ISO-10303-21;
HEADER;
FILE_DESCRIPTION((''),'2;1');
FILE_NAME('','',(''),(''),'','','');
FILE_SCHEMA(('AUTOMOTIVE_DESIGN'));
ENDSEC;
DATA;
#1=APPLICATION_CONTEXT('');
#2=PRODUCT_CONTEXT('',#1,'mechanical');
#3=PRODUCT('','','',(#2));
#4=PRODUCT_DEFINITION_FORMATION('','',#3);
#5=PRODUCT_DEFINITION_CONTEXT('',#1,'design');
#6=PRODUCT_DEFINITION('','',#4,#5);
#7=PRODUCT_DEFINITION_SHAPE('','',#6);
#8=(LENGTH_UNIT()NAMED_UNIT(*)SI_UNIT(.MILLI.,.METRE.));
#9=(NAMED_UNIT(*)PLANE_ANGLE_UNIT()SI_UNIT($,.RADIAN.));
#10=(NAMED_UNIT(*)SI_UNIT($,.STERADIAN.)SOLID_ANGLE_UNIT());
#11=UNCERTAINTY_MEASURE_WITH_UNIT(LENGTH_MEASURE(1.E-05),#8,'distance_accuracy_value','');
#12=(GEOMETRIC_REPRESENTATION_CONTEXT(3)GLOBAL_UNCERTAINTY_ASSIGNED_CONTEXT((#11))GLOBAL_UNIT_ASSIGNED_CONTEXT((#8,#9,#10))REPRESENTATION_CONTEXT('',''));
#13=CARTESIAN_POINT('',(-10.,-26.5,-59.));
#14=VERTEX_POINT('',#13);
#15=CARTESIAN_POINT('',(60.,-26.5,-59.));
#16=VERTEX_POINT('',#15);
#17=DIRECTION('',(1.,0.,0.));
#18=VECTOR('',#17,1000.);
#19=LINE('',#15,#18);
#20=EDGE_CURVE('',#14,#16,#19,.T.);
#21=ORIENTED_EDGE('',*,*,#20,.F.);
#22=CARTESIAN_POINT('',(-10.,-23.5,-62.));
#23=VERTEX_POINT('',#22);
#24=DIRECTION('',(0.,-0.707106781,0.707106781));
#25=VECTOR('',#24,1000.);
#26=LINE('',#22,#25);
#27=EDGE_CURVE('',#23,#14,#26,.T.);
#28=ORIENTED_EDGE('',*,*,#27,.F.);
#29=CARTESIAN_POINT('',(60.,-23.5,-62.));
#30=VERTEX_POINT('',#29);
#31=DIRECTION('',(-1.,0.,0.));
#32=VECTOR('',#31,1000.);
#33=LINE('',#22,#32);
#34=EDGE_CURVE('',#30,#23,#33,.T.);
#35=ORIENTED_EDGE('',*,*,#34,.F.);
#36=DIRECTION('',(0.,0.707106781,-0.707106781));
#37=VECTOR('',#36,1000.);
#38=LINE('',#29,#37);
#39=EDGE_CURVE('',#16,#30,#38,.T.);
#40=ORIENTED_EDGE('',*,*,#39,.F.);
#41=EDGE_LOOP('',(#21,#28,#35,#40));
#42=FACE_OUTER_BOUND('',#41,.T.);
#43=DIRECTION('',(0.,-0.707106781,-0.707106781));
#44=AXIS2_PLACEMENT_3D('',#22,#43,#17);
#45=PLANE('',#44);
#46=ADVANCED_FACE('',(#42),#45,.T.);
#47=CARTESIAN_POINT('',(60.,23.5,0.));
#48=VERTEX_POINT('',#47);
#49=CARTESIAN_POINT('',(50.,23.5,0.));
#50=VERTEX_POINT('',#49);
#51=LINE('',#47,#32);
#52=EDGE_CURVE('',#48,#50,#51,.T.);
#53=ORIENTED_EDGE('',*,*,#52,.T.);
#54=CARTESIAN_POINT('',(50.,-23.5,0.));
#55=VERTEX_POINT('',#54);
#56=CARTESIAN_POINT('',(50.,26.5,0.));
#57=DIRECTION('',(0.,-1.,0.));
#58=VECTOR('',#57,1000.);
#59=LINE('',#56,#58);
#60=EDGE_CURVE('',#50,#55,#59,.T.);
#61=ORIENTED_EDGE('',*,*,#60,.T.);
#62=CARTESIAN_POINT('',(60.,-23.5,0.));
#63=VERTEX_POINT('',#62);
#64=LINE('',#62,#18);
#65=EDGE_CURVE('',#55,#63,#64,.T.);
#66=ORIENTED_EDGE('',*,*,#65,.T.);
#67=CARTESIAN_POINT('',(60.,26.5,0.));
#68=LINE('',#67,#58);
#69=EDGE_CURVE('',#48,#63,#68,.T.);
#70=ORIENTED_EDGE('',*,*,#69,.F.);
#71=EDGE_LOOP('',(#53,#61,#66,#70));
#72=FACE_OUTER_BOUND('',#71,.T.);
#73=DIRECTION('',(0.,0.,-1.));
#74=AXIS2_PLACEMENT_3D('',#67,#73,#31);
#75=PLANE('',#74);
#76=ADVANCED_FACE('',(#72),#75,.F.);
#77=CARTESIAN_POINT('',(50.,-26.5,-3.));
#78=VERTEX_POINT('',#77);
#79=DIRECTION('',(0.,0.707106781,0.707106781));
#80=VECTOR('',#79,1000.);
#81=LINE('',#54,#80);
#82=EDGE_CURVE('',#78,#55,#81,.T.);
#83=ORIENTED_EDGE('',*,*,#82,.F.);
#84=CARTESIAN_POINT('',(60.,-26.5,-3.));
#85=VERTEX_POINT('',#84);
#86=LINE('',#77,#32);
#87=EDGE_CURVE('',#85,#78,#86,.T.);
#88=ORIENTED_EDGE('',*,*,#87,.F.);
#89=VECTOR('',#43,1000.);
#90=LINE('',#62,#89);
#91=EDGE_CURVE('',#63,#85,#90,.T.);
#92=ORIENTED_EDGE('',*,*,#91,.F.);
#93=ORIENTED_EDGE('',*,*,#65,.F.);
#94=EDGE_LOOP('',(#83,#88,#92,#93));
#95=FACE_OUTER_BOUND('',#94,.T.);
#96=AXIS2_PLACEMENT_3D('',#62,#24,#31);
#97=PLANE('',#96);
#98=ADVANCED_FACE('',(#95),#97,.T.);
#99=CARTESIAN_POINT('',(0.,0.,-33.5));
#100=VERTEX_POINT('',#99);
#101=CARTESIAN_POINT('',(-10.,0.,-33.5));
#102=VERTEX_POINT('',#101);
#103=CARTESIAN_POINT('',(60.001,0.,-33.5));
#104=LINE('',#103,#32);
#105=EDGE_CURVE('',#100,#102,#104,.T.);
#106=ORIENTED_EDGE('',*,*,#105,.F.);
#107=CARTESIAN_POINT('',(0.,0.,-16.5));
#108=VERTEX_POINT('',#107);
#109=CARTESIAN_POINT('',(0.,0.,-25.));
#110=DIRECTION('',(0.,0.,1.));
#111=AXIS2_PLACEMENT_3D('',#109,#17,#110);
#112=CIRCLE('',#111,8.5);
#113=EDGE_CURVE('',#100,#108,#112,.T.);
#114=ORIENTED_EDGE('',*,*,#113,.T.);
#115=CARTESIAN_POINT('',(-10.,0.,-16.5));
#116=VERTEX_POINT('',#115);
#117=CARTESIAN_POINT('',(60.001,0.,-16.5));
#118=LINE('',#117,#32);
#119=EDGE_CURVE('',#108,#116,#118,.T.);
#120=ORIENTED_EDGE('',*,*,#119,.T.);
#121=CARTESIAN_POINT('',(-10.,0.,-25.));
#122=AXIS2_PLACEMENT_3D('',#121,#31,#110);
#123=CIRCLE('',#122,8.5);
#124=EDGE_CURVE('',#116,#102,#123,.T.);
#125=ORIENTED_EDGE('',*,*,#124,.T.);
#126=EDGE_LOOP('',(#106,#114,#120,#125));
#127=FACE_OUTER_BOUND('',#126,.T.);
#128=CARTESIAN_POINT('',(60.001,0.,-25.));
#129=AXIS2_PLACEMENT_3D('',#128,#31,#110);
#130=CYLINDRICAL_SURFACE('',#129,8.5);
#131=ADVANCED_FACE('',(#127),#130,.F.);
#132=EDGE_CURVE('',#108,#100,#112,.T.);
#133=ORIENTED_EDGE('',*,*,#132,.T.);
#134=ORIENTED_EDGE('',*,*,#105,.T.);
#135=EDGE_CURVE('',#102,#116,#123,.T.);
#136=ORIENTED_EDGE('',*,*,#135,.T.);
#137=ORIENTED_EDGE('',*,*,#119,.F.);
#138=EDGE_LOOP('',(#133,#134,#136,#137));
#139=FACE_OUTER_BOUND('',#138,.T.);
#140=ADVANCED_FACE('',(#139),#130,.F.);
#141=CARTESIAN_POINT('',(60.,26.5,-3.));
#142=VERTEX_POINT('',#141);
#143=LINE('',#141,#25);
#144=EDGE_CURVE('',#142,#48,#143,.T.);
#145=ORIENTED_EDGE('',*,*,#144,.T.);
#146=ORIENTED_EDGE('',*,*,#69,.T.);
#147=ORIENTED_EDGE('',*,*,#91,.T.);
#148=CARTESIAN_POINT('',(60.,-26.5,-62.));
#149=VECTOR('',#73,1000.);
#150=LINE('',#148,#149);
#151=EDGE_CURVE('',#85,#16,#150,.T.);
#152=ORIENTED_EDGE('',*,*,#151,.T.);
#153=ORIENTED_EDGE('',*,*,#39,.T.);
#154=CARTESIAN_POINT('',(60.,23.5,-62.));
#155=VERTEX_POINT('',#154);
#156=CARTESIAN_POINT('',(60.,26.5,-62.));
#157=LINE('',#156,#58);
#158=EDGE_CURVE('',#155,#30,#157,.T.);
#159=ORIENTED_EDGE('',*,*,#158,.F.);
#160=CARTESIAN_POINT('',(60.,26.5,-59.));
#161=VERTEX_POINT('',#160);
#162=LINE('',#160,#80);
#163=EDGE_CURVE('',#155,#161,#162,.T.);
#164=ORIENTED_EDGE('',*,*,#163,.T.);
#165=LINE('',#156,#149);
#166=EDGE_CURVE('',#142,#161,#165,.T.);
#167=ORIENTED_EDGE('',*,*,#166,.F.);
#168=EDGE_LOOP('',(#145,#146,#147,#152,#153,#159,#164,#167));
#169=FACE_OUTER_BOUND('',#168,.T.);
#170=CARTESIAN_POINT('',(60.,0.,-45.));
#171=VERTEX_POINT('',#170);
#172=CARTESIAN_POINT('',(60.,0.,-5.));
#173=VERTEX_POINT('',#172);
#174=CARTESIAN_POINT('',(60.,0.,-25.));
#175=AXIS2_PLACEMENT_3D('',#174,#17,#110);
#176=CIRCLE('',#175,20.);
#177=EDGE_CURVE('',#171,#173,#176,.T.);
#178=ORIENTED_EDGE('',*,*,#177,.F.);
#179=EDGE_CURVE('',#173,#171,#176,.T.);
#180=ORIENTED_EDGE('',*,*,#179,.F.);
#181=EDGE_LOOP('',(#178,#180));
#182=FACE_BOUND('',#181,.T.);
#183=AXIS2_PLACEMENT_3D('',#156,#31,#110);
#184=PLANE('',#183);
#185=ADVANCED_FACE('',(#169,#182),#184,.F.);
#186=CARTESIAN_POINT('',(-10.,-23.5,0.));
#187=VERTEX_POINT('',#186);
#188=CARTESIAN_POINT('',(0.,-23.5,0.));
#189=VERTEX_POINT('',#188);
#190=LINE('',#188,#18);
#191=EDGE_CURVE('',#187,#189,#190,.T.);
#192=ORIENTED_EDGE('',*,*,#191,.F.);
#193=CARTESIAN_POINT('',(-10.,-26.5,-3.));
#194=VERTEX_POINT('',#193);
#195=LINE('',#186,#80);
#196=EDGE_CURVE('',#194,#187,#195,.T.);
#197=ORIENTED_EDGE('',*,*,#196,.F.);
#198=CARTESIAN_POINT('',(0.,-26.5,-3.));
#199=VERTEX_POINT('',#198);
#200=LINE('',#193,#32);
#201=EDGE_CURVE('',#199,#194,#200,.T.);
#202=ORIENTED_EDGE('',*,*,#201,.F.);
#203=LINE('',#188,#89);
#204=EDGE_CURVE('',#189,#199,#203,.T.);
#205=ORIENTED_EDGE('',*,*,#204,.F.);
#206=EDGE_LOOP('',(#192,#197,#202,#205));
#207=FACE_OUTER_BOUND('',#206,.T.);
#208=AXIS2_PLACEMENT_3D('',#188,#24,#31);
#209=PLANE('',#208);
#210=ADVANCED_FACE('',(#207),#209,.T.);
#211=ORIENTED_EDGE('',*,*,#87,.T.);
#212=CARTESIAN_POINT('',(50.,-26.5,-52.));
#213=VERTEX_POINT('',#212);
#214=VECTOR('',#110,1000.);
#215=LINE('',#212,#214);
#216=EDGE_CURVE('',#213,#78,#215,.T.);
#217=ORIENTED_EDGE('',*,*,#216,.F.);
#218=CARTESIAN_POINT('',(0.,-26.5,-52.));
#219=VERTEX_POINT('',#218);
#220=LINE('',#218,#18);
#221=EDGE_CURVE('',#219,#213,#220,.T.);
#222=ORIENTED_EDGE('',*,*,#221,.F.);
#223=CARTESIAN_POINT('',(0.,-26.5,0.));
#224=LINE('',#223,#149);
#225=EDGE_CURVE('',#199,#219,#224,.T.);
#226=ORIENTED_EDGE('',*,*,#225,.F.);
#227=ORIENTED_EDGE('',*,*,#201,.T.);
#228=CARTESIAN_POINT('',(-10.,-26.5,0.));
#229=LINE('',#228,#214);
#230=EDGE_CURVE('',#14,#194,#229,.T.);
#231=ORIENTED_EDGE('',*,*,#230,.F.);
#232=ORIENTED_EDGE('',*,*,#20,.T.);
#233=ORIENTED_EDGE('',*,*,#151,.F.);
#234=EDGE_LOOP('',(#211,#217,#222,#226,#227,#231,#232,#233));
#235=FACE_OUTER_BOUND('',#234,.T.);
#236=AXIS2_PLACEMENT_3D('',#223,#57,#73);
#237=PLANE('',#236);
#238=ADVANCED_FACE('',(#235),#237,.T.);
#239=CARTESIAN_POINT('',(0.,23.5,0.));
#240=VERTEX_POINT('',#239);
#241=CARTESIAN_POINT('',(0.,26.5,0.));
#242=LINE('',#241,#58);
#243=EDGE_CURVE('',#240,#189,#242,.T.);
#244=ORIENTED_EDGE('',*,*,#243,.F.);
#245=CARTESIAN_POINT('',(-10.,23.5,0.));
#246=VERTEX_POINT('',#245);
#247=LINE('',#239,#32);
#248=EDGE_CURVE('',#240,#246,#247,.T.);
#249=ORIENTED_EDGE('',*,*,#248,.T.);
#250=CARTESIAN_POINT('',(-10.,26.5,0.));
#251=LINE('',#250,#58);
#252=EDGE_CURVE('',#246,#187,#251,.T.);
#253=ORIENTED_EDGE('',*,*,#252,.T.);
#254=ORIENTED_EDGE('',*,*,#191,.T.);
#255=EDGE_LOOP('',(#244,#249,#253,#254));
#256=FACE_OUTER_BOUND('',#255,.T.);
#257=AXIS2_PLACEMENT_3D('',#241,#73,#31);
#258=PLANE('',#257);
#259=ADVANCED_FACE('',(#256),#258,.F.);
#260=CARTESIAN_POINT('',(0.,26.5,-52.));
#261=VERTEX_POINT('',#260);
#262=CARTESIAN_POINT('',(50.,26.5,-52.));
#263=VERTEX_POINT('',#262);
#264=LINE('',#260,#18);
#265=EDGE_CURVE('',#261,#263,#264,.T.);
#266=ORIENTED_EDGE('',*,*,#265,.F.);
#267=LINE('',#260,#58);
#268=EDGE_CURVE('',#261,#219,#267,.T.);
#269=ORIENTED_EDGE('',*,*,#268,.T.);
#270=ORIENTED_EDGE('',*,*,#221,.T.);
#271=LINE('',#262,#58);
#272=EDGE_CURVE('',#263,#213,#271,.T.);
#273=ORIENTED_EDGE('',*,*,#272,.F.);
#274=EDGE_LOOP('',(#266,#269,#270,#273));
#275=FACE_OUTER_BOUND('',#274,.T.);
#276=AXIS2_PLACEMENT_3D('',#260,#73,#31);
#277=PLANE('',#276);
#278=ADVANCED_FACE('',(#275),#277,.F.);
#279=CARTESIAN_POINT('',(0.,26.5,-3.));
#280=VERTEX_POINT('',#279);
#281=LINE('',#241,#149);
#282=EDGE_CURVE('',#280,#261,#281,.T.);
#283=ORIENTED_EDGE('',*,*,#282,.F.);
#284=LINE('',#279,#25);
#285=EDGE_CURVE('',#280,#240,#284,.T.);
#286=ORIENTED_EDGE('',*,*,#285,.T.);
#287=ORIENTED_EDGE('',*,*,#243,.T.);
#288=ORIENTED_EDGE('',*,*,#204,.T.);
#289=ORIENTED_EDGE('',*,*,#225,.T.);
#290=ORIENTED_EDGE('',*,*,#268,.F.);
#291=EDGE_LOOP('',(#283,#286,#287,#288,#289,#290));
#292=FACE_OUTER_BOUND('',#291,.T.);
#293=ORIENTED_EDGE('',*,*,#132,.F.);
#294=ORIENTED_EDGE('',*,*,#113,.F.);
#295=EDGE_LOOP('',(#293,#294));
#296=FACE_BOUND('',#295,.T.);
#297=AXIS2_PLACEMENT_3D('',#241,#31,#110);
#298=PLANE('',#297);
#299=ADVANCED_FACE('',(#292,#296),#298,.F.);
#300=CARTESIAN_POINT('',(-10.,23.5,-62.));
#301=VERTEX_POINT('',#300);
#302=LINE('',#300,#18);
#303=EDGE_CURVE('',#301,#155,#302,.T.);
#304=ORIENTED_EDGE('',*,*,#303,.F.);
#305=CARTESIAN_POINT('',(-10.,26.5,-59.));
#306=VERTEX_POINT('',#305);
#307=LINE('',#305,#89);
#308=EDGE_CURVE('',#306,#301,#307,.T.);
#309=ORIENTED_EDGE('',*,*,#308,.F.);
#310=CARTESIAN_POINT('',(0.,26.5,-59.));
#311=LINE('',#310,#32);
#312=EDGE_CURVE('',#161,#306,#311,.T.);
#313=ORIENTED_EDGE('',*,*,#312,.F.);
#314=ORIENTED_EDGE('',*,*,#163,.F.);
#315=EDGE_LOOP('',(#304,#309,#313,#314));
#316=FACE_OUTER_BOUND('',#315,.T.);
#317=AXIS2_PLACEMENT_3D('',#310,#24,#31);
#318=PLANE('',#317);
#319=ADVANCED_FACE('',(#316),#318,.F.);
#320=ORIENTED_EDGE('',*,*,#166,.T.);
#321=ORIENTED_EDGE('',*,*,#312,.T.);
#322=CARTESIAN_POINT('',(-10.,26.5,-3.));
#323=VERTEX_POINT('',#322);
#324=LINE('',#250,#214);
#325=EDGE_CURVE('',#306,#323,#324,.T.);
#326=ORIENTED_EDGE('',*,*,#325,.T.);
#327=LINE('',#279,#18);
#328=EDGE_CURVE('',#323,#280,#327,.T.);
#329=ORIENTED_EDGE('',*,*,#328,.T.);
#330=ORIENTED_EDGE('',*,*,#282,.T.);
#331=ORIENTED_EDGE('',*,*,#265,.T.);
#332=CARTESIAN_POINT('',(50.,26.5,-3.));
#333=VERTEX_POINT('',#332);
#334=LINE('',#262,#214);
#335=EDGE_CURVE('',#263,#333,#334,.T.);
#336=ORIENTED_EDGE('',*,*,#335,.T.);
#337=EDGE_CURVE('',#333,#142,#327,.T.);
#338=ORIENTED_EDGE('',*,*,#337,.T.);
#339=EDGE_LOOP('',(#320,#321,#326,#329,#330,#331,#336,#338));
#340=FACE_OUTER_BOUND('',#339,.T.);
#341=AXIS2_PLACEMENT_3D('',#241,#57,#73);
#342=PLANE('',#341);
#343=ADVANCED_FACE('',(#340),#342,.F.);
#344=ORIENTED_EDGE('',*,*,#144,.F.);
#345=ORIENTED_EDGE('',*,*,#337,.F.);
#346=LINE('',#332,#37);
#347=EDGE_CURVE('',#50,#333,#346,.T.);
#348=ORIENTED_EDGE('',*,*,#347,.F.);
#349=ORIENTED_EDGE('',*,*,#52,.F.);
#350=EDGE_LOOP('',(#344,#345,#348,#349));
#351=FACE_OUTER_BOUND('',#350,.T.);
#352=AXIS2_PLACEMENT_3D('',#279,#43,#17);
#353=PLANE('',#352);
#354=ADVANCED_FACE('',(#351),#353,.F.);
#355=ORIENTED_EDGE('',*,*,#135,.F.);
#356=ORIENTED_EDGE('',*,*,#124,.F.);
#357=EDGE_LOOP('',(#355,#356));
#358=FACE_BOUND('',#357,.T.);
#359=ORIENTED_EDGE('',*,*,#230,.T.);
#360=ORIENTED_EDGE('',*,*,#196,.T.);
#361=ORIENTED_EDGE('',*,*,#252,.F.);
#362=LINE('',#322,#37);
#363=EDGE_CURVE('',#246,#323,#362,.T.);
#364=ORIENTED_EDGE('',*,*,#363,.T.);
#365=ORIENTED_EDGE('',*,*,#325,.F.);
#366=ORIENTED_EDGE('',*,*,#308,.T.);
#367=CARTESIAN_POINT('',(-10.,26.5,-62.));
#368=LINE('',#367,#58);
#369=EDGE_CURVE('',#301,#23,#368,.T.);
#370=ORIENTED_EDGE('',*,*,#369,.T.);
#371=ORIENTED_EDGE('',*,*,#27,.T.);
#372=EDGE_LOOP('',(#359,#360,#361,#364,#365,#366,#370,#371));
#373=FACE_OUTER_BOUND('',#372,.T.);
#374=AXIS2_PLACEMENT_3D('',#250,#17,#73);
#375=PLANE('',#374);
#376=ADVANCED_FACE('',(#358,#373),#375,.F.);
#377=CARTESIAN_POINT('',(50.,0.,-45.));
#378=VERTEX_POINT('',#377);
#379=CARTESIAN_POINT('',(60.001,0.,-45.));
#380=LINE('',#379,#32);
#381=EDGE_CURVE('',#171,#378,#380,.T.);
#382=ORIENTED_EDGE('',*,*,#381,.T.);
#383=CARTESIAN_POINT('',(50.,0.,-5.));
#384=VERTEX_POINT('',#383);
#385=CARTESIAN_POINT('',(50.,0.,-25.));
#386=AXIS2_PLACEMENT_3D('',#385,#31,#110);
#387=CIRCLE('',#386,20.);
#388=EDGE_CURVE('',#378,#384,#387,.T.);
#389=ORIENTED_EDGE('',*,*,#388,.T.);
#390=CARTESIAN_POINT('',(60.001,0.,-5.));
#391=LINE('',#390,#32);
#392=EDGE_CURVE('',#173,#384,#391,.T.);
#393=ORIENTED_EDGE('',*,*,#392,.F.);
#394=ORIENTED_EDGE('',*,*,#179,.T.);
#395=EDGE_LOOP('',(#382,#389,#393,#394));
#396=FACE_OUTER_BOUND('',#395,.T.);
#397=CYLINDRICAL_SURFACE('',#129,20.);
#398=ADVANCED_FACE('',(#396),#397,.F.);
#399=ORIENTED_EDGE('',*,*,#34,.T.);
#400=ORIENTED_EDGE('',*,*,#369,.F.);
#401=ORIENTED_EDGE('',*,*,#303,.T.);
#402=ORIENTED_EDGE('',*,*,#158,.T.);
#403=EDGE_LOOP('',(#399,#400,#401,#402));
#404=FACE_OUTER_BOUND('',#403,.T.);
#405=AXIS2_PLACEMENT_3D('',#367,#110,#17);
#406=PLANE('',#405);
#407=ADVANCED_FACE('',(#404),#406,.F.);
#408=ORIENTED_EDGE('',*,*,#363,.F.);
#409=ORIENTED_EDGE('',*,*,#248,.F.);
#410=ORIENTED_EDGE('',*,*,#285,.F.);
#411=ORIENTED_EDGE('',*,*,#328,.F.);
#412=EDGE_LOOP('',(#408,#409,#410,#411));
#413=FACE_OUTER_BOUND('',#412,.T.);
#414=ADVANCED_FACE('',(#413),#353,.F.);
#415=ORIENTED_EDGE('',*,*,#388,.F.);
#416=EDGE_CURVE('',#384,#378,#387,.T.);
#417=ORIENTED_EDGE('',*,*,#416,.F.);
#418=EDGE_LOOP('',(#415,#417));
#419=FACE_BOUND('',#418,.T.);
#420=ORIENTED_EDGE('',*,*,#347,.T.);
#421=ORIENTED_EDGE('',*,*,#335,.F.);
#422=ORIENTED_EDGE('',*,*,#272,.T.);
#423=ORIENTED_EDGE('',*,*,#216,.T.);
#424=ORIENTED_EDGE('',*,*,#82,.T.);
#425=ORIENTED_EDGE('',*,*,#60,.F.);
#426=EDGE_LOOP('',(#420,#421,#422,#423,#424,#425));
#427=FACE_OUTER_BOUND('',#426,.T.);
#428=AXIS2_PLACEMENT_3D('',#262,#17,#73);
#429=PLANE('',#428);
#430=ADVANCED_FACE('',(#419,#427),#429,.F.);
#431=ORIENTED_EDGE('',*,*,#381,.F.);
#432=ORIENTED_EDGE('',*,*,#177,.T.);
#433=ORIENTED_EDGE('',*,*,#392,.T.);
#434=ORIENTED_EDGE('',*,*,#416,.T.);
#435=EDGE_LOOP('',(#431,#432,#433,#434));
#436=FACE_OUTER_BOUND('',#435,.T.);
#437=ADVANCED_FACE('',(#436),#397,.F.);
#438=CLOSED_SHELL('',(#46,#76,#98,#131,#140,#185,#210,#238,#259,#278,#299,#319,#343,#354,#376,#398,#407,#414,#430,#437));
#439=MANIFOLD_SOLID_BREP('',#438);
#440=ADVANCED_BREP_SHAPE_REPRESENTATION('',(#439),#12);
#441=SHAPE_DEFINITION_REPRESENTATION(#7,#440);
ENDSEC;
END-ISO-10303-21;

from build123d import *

# Parameters (mm, degrees)
EXTRUDE_1_DEPTH     = 26.5
CUT_EXTRUDE_2_REACH = 99.192
SKETCH_7_R          = 8.5
CUT_EXTRUDE_3_REACH = 92.257
SKETCH_8_R          = 20
CHAMFER_2_SIZE      = 3
CHAMFER_3_SIZE      = 3


with BuildPart() as part:
    # 草图1 → 凸台-拉伸1 (new, symmetric)
    with BuildSketch(Plane(origin=(0, 0, 0), x_dir=(1, 0, 0), z_dir=(0, 1, 0))):
        Polygon((0, 0), (0, 52), (50, 52), (50, 0), (60, 0), (60, 62), (-10, 62), (-10, 0), align=None)
    extrude(amount=EXTRUDE_1_DEPTH, both=True)

    # 草图7 → 切除-拉伸2 (cut, up to next)
    with BuildSketch(Plane.ZY.offset(10), mode=Mode.PRIVATE) as cut_extrude_2_sk1:
        with Locations((-25, 0)):
            Circle(SKETCH_7_R)
    cut_extrude_2_tool1 = extrude(cut_extrude_2_sk1.sketch, amount=-CUT_EXTRUDE_2_REACH, mode=Mode.PRIVATE) & part.part
    add(cut_extrude_2_tool1.solids().sort_by_distance((-10, 0, -25))[0], mode=Mode.SUBTRACT)

    # 草图8 → 切除-拉伸3 (cut, up to next)
    with BuildSketch(Plane.ZY.offset(-50), mode=Mode.PRIVATE) as cut_extrude_3_sk1:
        with Locations((-25, 0)):
            Circle(SKETCH_8_R)
    cut_extrude_3_tool1 = extrude(cut_extrude_3_sk1.sketch, amount=-CUT_EXTRUDE_3_REACH, mode=Mode.PRIVATE) & part.part
    add(cut_extrude_3_tool1.solids().sort_by_distance((50, 0, -25))[0], mode=Mode.SUBTRACT)

    # 倒角2
    chamfer_2_edges = [part.edges().sort_by_distance(p)[0] for p in [
        (25, 26.5, -62),
        (25, -26.5, -62),
    ]]
    chamfer(chamfer_2_edges, length=CHAMFER_2_SIZE)

    # 倒角3
    chamfer_3_edges = [part.edges().sort_by_distance(p)[0] for p in [
        (-5, -26.5, 0),
        (55, 26.5, 0),
        (-5, 26.5, 0),
        (55, -26.5, 0),
    ]]
    chamfer(chamfer_3_edges, length=CHAMFER_3_SIZE)


solid = part.part
